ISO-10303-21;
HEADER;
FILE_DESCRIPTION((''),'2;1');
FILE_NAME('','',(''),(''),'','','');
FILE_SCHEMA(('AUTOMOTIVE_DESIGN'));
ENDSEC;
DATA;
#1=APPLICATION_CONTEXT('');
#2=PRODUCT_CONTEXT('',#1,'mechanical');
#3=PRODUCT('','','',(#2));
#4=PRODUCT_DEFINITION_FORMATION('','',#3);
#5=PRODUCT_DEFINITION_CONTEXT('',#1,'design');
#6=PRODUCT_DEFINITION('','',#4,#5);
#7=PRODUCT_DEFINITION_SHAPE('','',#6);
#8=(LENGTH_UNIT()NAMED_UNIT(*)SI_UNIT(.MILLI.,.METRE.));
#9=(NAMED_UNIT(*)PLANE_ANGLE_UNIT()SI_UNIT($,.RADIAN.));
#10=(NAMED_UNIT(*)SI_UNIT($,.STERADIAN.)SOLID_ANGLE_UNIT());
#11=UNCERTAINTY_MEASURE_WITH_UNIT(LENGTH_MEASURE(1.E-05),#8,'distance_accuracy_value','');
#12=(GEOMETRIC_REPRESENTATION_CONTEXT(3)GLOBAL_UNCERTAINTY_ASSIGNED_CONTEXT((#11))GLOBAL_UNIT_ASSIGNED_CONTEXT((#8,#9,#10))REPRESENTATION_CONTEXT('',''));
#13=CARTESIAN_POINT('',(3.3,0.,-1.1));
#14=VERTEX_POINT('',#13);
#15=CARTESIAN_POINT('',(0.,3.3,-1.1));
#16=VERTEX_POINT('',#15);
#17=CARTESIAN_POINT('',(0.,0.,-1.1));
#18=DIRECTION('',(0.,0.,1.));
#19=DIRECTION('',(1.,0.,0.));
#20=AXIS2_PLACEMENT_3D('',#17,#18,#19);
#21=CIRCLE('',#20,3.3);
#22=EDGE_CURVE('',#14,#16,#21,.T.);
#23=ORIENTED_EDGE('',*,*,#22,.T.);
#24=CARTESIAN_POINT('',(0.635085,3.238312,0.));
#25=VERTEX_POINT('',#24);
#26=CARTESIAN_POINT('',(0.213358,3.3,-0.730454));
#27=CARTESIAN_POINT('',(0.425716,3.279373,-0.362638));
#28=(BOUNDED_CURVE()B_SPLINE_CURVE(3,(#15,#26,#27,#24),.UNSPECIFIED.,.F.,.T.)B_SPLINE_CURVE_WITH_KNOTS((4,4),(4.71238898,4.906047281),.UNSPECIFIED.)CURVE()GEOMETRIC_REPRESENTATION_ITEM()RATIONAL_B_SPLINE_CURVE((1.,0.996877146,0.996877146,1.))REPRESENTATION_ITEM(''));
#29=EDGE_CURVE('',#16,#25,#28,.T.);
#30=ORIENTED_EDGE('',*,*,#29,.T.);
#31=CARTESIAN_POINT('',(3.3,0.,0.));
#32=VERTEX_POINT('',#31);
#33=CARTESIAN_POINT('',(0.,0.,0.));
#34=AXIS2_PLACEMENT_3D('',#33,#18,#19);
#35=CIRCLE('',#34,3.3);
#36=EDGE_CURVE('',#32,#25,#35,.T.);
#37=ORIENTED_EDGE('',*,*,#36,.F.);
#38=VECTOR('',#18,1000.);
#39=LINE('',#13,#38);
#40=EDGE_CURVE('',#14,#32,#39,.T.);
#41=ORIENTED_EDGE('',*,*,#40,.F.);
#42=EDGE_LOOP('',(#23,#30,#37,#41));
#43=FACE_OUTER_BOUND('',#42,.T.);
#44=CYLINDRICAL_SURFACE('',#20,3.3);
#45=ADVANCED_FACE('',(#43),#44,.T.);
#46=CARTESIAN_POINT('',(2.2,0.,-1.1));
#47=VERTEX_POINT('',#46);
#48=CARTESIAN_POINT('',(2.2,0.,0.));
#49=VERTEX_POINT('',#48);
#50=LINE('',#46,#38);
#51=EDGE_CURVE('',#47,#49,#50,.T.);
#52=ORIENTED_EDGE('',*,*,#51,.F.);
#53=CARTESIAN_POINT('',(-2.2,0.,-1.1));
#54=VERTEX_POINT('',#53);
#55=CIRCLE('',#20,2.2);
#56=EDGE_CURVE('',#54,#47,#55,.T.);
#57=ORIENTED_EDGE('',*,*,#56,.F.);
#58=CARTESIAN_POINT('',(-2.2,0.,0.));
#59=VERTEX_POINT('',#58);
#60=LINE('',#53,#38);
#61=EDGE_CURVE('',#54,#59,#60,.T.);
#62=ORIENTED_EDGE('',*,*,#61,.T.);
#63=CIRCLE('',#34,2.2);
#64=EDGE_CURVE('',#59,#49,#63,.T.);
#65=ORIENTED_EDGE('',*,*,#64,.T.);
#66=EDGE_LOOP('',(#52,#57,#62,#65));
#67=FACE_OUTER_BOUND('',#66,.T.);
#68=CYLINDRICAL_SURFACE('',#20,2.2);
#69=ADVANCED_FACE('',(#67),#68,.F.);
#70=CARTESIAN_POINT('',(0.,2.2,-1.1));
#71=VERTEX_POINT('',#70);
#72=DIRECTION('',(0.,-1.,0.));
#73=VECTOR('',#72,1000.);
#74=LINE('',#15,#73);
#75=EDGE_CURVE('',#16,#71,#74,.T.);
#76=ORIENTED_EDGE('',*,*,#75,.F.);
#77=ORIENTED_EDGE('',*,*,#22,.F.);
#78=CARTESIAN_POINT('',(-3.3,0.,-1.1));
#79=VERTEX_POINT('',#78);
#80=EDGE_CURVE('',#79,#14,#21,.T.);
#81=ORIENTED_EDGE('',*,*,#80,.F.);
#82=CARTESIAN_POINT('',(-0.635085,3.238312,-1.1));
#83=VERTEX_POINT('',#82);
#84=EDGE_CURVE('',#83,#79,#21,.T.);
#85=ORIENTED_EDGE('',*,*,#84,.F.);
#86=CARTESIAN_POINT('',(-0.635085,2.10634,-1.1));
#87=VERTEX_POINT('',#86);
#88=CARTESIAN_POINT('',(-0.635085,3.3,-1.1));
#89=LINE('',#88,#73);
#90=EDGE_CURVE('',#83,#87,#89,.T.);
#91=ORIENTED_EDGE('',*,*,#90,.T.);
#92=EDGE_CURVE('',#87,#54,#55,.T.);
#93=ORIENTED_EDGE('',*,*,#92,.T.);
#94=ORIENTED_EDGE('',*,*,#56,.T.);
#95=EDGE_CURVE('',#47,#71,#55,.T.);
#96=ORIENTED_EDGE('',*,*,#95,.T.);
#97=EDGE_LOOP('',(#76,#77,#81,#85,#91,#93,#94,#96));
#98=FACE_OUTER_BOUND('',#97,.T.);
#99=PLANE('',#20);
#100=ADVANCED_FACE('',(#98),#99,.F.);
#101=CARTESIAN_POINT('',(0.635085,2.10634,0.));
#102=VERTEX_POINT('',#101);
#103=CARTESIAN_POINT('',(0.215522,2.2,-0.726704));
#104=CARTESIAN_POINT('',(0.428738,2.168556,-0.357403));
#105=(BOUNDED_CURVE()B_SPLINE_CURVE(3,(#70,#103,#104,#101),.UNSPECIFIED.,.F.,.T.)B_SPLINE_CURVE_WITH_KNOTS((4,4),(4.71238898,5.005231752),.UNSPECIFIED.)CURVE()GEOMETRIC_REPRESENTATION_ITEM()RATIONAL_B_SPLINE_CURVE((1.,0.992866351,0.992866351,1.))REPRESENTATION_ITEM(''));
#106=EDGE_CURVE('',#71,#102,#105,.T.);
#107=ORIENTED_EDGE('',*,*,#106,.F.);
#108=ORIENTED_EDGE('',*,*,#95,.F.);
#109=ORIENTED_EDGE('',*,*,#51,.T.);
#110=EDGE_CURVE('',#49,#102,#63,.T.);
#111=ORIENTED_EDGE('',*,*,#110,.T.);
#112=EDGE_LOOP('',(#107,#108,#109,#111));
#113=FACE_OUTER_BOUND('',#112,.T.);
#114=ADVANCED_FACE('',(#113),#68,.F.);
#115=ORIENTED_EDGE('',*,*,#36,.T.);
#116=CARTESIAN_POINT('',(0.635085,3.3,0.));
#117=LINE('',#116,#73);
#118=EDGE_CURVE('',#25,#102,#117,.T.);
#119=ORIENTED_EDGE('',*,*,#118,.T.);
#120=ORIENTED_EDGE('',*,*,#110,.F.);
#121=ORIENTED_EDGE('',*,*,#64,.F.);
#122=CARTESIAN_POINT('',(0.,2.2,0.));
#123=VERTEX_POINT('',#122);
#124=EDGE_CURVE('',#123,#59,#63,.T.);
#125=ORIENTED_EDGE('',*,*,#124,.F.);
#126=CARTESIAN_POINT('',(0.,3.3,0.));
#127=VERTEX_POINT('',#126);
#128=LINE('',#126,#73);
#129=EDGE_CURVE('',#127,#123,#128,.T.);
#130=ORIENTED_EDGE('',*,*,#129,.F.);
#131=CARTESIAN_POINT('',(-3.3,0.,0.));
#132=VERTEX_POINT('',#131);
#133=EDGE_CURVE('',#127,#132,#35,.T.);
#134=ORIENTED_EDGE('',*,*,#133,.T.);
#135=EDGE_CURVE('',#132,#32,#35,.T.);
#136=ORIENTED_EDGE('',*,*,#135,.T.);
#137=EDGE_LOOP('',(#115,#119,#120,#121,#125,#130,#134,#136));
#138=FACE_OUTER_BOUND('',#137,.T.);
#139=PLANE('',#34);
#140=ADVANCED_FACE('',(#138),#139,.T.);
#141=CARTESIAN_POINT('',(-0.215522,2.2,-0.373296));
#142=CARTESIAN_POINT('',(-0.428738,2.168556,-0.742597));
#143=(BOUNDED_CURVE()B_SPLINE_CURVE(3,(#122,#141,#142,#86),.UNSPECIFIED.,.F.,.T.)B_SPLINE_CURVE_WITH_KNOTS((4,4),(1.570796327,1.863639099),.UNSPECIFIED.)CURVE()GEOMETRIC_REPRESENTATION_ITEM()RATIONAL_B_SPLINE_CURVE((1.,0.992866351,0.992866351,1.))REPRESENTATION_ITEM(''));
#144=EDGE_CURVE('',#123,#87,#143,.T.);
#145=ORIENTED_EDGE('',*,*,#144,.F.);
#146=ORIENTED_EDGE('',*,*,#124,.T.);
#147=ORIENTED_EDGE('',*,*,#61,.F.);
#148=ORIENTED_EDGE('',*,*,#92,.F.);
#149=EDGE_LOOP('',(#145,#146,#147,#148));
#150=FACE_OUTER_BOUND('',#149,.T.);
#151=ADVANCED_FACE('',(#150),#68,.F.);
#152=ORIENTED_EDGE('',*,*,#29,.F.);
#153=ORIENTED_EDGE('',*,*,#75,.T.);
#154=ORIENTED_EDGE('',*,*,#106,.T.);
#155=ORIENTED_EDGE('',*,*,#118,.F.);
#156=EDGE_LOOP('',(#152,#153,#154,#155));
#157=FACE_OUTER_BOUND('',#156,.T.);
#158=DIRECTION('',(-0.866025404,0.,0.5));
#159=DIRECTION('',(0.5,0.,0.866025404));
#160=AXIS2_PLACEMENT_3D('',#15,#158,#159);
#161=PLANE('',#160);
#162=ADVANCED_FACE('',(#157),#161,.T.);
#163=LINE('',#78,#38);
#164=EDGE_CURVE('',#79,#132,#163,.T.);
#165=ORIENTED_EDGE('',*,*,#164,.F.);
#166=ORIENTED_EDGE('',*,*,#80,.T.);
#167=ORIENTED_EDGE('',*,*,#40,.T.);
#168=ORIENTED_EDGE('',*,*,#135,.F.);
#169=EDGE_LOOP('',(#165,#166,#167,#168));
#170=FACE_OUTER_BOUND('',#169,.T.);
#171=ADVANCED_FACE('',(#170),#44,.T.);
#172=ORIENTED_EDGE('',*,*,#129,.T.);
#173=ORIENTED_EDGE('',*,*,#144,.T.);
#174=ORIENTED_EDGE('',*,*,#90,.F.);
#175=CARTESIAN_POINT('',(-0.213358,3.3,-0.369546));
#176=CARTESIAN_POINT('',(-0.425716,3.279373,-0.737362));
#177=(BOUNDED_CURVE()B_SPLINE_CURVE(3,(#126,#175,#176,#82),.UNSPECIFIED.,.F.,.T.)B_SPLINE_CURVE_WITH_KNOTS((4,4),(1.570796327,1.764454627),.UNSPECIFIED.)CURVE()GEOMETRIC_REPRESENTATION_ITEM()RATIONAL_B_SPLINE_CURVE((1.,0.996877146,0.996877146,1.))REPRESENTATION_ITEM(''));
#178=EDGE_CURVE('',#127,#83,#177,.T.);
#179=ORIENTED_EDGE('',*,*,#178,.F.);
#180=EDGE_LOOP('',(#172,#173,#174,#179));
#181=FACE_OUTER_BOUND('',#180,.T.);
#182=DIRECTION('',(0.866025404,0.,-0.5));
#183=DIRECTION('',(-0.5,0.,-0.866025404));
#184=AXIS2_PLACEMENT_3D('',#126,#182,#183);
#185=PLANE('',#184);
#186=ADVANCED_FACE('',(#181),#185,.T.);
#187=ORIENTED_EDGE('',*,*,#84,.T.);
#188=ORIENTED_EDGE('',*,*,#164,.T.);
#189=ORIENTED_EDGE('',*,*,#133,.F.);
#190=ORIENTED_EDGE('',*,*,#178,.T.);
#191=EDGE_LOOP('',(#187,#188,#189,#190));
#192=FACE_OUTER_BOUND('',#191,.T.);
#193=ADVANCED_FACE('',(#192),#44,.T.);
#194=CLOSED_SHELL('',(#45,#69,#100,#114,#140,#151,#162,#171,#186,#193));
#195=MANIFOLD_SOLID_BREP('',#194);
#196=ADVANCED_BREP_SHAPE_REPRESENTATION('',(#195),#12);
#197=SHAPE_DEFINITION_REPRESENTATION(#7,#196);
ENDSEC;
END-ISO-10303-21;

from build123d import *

# Parameters (mm, degrees)
SKETCH1_R          = 3.3
SKETCH1_R_2        = 2.2
BASE_EXTRUDE_DEPTH = 1.1
CUT_EXTRUDE1_DEPTH = 5.794788838


with BuildPart() as part:
    # Sketch1 → Base-Extrude (new body)
    with BuildSketch(Plane.XY):
        Circle(SKETCH1_R)
        Circle(SKETCH1_R_2, mode=Mode.SUBTRACT)
    extrude(amount=-BASE_EXTRUDE_DEPTH)

    # Sketch2 → Cut-Extrude1 (cut, through all)
    with BuildSketch(Plane(origin=(0, 0, 0), x_dir=(1, 0, 0), z_dir=(0, 1, 0))):
        Polygon((0, 1.1), (0.635085296, 0), (0, 0), (-0.635085296, 1.1), align=None)
    extrude(amount=CUT_EXTRUDE1_DEPTH, mode=Mode.SUBTRACT)


solid = part.part
